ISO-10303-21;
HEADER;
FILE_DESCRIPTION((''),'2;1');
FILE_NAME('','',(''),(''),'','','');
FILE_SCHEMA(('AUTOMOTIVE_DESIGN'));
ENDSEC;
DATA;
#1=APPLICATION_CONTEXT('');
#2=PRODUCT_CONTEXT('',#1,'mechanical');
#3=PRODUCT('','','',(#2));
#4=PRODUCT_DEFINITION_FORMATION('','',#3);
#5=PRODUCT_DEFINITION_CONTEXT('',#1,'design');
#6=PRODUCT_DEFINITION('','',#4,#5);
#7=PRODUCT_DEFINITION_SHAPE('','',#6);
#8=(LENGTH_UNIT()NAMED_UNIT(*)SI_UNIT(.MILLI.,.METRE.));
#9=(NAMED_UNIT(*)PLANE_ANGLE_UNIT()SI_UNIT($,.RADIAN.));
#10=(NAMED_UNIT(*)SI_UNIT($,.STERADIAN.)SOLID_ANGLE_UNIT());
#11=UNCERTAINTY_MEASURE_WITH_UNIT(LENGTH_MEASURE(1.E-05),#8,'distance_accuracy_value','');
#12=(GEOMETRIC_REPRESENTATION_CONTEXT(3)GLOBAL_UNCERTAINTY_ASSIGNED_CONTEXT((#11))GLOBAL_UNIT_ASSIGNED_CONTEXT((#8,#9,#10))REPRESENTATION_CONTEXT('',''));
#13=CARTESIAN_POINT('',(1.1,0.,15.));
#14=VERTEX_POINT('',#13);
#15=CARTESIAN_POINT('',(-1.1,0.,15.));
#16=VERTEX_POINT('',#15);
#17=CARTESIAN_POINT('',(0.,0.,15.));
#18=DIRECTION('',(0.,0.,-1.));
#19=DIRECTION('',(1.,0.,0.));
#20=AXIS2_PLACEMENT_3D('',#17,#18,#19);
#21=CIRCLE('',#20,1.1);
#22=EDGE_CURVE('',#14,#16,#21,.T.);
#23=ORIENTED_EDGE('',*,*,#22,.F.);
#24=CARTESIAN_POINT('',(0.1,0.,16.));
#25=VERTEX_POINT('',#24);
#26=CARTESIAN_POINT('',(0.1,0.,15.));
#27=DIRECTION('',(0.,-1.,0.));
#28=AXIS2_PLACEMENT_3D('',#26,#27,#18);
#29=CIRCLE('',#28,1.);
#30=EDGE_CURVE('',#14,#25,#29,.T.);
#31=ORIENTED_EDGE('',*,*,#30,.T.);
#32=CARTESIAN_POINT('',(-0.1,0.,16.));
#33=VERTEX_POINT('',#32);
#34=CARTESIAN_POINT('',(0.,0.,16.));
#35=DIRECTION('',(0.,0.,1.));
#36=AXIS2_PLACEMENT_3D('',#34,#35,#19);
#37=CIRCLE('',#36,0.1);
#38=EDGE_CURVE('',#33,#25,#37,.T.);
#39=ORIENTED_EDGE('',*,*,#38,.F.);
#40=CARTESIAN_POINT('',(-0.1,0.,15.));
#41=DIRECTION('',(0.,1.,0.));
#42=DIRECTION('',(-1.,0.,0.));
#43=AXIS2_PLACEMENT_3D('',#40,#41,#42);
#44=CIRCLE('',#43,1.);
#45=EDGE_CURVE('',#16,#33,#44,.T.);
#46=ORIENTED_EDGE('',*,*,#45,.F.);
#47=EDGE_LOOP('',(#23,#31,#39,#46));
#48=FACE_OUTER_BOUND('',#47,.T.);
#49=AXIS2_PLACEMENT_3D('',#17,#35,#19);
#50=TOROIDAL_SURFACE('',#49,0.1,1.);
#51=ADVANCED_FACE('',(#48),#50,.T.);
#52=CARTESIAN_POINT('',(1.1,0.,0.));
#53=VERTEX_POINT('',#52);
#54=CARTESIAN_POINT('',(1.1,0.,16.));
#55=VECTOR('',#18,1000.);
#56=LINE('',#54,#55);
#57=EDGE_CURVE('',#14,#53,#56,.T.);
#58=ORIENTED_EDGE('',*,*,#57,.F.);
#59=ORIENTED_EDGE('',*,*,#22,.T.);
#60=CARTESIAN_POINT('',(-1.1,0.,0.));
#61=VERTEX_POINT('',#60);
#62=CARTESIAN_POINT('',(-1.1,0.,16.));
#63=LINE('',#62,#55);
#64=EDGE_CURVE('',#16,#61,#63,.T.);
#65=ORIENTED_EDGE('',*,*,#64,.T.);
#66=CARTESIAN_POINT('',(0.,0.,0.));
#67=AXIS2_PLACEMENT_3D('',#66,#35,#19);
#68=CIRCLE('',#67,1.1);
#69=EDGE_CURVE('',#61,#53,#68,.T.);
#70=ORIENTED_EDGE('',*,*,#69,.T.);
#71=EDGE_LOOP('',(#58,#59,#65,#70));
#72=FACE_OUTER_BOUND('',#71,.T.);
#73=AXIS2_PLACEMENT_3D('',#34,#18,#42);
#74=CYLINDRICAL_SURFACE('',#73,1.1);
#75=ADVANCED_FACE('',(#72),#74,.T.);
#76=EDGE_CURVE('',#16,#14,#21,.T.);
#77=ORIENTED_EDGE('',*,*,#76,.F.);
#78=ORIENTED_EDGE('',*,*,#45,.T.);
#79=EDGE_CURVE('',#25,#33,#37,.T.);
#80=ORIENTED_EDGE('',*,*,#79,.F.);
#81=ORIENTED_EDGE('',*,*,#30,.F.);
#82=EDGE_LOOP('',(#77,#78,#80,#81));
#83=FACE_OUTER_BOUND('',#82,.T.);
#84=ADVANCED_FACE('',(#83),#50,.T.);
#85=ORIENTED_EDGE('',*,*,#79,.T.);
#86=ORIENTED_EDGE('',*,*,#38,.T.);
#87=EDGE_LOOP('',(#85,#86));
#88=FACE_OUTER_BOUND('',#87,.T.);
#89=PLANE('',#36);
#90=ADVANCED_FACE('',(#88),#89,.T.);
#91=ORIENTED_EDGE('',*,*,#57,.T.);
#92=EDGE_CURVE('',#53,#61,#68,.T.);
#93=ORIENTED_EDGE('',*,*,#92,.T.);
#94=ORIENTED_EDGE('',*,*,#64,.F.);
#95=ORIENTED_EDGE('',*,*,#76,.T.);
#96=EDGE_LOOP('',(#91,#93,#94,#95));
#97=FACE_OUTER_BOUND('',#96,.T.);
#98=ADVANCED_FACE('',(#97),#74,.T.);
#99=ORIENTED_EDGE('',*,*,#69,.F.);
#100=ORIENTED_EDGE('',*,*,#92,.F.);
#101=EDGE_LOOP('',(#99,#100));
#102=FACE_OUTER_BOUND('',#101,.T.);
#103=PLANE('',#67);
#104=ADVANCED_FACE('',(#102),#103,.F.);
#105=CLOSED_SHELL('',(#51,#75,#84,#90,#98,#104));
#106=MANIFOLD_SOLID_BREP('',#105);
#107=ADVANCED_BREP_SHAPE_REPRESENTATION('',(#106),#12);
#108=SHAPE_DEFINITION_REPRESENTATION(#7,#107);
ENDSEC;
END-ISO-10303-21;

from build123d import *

# Parameters (mm, degrees)
SKETCH1_R           = 1.1
BOSS_EXTRUDE1_DEPTH = 16
FILLET1_R           = 1


with BuildPart() as part:
    # Sketch1 → Boss-Extrude1 (new body)
    with BuildSketch(Plane.XY):
        Circle(SKETCH1_R)
    extrude(amount=BOSS_EXTRUDE1_DEPTH)

    # Fillet1
    fillet1_edges = [part.edges().sort_by_distance(p)[0] for p in [
        (-1.1, 0, 16),
    ]]
    fillet(fillet1_edges, radius=FILLET1_R)


solid = part.part
